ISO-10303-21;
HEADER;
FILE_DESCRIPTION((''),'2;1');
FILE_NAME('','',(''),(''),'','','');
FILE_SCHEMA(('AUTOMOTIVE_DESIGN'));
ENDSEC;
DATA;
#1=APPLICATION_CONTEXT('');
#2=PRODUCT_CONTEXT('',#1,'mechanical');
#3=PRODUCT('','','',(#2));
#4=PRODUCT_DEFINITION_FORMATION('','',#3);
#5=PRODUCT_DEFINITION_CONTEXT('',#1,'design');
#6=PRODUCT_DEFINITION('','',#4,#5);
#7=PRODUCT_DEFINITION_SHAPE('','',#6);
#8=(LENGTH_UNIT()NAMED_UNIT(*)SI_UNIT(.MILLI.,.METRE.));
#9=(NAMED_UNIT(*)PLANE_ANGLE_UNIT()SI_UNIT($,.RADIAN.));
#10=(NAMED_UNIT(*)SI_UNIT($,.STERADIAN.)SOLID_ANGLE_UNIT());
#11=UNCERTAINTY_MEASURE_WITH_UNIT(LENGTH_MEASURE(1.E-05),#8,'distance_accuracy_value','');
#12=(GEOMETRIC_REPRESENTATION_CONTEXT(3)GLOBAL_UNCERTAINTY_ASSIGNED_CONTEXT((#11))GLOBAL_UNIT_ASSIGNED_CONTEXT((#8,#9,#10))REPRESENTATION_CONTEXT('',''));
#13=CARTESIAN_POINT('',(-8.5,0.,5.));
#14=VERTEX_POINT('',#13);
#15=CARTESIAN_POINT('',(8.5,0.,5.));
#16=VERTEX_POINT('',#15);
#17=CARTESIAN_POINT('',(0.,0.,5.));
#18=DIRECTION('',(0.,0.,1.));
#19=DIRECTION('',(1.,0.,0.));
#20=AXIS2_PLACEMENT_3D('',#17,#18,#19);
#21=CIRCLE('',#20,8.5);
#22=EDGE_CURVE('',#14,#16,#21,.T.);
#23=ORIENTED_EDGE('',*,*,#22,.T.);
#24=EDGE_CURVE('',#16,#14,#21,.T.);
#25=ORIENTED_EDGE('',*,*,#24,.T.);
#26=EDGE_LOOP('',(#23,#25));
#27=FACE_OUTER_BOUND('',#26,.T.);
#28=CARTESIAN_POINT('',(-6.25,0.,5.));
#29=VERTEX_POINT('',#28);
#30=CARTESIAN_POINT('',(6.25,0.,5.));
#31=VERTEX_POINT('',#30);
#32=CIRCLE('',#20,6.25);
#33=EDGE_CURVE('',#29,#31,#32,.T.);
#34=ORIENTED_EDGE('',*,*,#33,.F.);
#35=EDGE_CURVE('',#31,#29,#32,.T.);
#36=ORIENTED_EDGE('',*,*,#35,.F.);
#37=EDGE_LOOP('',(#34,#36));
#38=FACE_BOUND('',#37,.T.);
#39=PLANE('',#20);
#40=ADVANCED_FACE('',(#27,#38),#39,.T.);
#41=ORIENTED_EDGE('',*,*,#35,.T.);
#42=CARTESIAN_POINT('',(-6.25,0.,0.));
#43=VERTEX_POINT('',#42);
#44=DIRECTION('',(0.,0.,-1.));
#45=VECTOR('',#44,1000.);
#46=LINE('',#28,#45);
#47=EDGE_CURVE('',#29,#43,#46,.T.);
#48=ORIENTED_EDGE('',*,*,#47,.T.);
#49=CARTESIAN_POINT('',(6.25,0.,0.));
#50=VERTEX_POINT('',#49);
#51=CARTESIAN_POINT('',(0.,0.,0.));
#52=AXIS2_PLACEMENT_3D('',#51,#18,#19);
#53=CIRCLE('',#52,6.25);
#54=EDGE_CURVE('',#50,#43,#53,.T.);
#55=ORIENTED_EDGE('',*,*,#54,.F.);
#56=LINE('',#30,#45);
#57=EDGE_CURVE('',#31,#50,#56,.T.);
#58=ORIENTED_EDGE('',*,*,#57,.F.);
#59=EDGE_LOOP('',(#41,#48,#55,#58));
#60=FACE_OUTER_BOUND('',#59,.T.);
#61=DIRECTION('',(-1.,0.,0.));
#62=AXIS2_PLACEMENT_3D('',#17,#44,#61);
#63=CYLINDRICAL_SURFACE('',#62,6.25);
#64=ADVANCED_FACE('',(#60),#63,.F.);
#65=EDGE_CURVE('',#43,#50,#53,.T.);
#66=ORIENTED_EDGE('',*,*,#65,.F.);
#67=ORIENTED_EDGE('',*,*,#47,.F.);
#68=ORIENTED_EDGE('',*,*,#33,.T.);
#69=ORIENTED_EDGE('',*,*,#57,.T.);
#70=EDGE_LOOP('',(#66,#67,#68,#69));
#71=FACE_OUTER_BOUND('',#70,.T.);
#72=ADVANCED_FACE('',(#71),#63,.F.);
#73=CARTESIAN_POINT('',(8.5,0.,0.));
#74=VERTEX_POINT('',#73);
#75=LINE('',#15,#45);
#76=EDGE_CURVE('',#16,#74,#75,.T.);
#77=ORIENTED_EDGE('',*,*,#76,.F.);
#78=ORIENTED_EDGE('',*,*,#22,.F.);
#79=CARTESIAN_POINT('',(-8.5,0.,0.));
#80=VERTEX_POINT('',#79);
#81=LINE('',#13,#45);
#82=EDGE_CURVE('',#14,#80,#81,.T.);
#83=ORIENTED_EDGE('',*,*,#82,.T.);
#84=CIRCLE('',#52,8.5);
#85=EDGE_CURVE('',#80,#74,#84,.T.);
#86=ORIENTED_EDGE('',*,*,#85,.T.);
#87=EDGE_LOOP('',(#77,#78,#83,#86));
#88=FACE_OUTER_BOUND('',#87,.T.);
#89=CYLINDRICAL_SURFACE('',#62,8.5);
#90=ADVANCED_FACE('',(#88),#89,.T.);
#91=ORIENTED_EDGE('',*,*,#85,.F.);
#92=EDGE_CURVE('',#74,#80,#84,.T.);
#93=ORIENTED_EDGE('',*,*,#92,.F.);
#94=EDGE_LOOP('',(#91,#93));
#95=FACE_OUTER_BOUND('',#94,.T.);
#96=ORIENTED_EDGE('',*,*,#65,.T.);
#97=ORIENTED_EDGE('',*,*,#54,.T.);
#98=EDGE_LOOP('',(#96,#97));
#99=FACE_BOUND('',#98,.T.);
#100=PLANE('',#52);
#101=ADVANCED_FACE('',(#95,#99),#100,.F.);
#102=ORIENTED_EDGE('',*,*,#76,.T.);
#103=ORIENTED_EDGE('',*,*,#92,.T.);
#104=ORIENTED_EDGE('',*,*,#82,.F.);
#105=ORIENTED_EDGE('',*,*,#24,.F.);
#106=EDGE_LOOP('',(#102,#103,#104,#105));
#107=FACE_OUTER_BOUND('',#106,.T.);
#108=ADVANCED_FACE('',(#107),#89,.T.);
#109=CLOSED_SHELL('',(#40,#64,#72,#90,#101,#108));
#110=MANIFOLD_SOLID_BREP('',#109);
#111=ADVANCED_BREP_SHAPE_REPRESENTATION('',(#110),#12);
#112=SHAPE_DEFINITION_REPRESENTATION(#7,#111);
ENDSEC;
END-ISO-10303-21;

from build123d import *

# Parameters (mm, degrees)
SKETCH_1_R      = 8.5
SKETCH_1_R_2    = 6.25
EXTRUDE_1_DEPTH = 5


with BuildPart() as part:
    # 草图1 → 凸台-拉伸1 (new body)
    with BuildSketch(Plane.XY):
        Circle(SKETCH_1_R)
        Circle(SKETCH_1_R_2, mode=Mode.SUBTRACT)
    extrude(amount=EXTRUDE_1_DEPTH)


solid = part.part
